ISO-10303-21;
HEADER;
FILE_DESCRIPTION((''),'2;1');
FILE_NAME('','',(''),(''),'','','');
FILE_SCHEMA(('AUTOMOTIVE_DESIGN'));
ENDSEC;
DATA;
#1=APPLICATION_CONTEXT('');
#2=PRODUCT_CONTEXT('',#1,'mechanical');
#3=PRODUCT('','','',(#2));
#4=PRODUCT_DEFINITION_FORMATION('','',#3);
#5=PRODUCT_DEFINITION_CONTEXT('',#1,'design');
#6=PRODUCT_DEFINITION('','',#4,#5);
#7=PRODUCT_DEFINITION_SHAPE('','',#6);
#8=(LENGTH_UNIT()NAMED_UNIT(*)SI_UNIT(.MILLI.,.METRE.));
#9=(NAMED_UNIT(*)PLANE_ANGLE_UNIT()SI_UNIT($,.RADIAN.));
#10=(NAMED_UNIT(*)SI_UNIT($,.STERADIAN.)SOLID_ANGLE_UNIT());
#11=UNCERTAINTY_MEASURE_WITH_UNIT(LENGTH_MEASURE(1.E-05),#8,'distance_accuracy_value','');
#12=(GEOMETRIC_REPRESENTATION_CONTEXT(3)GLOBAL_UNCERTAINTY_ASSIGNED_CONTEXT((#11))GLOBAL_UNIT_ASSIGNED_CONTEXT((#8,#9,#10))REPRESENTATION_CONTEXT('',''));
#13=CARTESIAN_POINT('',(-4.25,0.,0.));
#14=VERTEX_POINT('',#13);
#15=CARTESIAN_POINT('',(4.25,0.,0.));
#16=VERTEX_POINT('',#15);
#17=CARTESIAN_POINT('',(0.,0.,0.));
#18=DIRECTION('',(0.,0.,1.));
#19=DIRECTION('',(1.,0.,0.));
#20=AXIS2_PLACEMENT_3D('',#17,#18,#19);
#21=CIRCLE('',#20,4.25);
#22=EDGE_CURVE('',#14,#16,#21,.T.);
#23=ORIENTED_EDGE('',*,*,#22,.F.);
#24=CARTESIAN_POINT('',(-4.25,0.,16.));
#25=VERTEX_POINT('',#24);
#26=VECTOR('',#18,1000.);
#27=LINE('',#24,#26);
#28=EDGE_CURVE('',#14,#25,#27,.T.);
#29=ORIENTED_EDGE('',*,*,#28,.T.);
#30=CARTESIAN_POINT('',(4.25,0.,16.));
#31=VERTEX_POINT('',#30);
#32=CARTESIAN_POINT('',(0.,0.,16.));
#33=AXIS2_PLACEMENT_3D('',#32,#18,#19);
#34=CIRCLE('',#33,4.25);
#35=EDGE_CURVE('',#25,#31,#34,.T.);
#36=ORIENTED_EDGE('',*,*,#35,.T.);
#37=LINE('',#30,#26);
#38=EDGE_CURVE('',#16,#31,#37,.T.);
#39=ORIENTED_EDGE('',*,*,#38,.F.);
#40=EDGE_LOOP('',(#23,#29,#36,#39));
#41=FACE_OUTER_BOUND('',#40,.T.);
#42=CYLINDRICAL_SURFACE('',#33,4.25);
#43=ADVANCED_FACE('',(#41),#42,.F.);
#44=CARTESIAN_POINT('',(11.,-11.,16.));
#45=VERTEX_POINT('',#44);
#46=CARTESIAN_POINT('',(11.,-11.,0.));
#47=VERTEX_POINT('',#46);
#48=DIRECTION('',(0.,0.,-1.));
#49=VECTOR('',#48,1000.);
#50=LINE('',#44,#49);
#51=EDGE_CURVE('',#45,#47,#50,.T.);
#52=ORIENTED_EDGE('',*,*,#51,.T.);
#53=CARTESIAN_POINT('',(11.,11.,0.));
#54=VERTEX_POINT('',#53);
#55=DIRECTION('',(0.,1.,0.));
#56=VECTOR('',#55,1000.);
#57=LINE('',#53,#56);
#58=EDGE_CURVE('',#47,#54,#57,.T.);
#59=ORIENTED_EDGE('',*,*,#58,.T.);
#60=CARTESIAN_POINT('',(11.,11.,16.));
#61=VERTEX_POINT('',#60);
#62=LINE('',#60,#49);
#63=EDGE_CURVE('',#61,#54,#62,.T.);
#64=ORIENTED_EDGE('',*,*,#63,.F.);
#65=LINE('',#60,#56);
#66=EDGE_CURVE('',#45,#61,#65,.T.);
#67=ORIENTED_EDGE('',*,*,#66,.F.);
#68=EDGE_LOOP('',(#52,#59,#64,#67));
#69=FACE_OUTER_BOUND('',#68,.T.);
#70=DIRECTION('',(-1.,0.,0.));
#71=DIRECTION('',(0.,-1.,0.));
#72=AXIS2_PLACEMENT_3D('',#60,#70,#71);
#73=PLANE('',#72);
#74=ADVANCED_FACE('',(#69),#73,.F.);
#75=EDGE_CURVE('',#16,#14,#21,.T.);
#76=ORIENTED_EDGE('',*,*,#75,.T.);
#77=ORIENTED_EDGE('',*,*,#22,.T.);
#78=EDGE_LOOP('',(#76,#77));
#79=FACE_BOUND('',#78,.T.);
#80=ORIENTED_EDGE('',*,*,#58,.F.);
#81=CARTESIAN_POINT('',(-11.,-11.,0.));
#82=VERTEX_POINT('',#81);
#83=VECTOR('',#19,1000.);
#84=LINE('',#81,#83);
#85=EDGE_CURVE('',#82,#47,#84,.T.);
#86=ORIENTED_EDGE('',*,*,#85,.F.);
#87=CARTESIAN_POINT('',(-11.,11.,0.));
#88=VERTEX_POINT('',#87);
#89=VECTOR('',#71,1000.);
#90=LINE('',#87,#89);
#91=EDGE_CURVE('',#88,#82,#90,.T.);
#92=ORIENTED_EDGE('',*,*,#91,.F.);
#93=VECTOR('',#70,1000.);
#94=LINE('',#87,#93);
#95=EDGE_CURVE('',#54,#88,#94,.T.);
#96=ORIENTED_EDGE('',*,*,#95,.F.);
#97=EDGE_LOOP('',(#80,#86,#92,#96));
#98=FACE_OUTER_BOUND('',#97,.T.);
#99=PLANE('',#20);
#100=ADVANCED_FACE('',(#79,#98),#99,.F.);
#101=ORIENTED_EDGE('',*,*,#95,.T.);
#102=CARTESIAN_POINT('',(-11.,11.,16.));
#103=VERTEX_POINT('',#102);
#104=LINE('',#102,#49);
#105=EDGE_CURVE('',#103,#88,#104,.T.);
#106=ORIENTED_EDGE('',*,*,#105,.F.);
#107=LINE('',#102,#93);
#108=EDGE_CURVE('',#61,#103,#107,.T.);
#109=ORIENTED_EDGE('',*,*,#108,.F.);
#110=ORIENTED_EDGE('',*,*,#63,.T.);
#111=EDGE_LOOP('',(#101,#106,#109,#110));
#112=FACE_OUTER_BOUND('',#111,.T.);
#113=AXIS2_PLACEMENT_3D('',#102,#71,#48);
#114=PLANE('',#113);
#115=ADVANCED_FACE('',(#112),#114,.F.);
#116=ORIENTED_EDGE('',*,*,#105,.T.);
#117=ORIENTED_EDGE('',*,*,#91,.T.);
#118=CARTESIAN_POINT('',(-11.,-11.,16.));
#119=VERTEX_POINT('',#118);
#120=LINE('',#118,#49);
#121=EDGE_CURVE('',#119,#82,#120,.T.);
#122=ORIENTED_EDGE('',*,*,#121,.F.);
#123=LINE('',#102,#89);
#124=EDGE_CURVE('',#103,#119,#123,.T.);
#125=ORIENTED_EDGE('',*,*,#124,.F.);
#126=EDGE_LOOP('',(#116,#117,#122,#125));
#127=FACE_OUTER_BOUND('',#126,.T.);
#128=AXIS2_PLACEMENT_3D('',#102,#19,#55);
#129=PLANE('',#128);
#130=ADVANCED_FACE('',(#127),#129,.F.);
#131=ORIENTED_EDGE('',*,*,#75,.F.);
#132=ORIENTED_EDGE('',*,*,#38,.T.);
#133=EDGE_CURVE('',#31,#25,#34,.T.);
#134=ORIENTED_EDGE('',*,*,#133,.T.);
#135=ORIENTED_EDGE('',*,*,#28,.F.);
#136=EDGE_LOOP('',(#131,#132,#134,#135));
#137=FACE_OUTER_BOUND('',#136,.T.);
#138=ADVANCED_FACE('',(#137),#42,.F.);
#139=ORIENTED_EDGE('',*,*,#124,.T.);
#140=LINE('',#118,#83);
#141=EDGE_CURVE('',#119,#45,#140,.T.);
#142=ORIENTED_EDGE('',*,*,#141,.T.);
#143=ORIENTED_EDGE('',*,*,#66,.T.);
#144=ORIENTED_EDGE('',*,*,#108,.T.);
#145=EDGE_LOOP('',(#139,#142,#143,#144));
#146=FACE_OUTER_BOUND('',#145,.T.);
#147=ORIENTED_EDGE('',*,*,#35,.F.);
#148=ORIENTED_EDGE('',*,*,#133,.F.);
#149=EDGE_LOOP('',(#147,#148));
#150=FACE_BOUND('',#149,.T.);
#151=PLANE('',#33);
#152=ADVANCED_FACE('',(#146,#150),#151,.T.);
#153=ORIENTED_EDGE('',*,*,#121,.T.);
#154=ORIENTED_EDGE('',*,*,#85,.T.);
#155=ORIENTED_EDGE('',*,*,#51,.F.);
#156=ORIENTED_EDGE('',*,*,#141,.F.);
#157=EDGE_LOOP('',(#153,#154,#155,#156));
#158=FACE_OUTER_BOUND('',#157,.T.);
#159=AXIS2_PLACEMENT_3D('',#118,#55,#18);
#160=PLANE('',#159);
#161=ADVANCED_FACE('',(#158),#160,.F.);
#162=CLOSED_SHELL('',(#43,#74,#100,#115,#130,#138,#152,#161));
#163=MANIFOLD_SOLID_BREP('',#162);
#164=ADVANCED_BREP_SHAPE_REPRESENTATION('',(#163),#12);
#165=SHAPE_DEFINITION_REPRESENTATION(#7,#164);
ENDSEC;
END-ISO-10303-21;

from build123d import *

# Parameters (mm, degrees)
SKETCH1_W              = 22
SKETCH1_H              = 22
BOSS_EXTRUDE1_DEPTH    = 16
M10_TAPPED_HOLE1_D     = 8.5
M10_TAPPED_HOLE1_DEPTH = 27.5
M10_TAPPED_HOLE1_TIP   = 2.553657631


with BuildPart() as part:
    # Sketch1 → Boss-Extrude1 (new body)
    with BuildSketch(Plane.XY):
        Rectangle(SKETCH1_W, SKETCH1_H)
    extrude(amount=BOSS_EXTRUDE1_DEPTH)

    # M10 Tapped Hole1
    with Locations(Plane.XY.offset(16)):
        with Locations((0, 0)):
            Hole(M10_TAPPED_HOLE1_D / 2, depth=M10_TAPPED_HOLE1_DEPTH)
            with Locations((0, 0, -(M10_TAPPED_HOLE1_DEPTH + M10_TAPPED_HOLE1_TIP / 2))):  # 118° drill point
                Cone(0, M10_TAPPED_HOLE1_D / 2, M10_TAPPED_HOLE1_TIP, mode=Mode.SUBTRACT)


solid = part.part
